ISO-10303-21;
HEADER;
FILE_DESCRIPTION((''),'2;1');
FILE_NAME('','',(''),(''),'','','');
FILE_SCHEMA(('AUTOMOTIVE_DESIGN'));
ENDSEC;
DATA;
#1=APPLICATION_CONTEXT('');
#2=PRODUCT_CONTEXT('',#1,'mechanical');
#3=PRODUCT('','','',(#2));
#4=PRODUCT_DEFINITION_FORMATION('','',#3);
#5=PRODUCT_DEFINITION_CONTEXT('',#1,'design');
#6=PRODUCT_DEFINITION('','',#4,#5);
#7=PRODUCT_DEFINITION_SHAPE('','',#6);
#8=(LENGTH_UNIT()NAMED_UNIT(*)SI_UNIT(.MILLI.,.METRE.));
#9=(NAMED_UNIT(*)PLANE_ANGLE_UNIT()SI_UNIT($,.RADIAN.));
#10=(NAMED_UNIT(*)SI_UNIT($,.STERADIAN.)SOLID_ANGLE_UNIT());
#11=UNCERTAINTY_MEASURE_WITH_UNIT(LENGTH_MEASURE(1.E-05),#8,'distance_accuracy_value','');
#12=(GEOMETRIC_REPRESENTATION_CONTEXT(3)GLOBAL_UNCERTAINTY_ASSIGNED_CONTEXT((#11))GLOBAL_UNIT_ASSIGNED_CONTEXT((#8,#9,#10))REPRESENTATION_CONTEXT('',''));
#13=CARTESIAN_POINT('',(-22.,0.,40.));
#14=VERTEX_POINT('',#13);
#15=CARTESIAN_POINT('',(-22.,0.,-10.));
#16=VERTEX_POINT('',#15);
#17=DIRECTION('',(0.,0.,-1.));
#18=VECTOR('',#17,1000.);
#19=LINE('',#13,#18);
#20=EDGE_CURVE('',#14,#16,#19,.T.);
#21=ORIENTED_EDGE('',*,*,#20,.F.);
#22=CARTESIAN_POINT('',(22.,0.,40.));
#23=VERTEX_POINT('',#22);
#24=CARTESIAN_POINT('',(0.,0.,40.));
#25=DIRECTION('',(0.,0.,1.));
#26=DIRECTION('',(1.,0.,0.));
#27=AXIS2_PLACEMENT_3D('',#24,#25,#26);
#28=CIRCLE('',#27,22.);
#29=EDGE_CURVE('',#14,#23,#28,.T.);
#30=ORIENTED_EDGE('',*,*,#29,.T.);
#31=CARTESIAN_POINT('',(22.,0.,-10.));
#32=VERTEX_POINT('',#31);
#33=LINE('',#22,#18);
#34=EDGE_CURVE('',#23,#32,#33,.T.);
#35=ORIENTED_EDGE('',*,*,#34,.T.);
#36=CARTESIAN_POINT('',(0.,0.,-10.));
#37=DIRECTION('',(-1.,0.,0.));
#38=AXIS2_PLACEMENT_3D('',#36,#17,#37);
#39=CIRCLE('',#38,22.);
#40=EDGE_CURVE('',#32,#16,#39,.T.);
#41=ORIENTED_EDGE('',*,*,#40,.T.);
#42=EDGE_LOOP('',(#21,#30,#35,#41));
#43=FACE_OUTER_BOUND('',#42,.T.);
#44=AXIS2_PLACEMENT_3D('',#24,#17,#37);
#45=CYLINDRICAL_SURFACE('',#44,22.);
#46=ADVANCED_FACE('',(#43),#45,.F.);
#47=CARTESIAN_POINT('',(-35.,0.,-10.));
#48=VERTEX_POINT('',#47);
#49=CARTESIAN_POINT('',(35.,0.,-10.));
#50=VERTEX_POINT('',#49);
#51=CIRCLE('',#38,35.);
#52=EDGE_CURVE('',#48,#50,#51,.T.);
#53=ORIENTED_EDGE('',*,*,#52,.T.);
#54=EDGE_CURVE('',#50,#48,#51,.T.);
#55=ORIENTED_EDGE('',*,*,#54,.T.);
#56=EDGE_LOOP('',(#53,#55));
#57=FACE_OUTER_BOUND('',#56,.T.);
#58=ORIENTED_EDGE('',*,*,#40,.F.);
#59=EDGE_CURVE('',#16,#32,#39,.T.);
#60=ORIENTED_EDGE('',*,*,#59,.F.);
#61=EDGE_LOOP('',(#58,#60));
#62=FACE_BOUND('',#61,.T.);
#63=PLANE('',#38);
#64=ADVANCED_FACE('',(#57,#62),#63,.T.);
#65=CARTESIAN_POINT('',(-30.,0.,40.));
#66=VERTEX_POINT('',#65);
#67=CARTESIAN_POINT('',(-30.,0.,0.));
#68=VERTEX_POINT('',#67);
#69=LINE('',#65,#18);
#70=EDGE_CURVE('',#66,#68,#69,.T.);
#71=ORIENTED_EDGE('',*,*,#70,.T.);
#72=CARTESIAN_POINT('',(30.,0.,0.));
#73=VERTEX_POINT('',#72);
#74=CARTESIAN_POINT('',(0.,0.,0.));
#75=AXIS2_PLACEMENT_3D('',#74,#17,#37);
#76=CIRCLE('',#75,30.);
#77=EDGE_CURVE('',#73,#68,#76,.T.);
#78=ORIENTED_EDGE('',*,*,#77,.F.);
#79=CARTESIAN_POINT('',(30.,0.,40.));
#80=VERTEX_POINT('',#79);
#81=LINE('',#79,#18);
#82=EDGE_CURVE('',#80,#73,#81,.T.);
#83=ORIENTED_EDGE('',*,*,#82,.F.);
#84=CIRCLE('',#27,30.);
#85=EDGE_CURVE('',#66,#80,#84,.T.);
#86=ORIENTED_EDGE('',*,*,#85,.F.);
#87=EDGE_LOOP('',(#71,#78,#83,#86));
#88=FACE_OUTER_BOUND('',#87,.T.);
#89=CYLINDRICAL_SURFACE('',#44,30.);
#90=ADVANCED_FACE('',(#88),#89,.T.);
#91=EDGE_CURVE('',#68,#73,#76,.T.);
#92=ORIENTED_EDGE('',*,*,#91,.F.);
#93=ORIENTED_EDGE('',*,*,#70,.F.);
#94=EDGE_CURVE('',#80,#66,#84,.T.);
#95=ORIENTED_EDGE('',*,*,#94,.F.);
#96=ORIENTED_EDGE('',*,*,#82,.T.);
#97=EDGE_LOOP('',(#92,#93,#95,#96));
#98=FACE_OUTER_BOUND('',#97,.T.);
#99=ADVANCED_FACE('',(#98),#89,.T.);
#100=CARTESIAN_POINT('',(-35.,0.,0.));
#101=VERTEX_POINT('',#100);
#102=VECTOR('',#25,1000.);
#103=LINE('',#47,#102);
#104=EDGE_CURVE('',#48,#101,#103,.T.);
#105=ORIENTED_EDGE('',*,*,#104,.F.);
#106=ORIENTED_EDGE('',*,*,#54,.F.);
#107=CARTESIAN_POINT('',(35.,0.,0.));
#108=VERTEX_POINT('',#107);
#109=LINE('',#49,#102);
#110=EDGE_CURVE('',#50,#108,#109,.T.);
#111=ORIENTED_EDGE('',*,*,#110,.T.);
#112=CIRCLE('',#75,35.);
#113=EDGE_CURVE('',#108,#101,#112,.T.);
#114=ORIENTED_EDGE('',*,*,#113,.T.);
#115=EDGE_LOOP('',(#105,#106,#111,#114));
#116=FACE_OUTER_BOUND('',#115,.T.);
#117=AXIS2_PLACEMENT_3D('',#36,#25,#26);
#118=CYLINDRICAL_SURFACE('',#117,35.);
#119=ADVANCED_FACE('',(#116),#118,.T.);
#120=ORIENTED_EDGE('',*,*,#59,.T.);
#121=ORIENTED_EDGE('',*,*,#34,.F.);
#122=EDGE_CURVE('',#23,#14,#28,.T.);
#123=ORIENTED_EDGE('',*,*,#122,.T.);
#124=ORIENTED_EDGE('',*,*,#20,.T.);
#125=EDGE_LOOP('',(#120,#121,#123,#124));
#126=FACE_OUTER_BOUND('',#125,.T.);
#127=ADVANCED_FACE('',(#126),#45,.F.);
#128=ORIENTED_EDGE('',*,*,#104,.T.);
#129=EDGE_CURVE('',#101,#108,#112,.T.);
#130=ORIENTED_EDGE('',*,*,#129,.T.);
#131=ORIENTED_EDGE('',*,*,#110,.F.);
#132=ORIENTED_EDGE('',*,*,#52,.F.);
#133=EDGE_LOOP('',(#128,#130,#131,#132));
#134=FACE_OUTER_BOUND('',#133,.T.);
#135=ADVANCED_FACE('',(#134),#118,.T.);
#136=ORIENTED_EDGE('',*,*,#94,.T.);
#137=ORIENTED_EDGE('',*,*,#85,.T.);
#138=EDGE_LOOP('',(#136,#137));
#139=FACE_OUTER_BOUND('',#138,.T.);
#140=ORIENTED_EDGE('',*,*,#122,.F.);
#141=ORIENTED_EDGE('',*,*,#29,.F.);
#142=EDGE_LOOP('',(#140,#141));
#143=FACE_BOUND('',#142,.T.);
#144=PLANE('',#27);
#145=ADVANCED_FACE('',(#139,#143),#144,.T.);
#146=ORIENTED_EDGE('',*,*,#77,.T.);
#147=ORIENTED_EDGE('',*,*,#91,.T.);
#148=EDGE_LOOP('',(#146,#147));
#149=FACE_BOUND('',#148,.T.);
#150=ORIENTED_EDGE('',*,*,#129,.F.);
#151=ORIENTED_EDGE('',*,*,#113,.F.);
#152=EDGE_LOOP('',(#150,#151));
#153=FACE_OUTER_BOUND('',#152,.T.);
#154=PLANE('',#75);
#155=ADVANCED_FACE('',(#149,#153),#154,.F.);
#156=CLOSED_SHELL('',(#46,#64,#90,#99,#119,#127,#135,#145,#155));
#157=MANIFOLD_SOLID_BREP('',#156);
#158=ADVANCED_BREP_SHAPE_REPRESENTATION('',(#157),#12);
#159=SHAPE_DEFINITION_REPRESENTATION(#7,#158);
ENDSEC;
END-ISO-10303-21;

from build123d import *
from build123d.topology import SkipClean

# Parameters (mm, degrees)
SKETCH1_R           = 30
SKETCH1_R_2         = 22
BOSS_EXTRUDE1_DEPTH = 40
BOSS_EXTRUDE2_START = 10
SKETCH2_R           = 35
SKETCH2_R_2         = 22
BOSS_EXTRUDE2_DEPTH = 10


with BuildPart() as part:
    # Sketch1 → Boss-Extrude1 (new body)
    with BuildSketch(Plane.XY):
        Circle(SKETCH1_R)
        Circle(SKETCH1_R_2, mode=Mode.SUBTRACT)
    extrude(amount=BOSS_EXTRUDE1_DEPTH)

    # Sketch2 → Boss-Extrude2 (add)
    with SkipClean():  # the faces are left unmerged after this step: merging them gives an invalid solid
        with BuildSketch(Plane(origin=(0, 0, 0), x_dir=(-1, 0, 0), z_dir=(0, 0, -1)).offset(BOSS_EXTRUDE2_START)):
            Circle(SKETCH2_R)
            Circle(SKETCH2_R_2, mode=Mode.SUBTRACT)
        extrude(amount=-BOSS_EXTRUDE2_DEPTH)


solid = part.part
